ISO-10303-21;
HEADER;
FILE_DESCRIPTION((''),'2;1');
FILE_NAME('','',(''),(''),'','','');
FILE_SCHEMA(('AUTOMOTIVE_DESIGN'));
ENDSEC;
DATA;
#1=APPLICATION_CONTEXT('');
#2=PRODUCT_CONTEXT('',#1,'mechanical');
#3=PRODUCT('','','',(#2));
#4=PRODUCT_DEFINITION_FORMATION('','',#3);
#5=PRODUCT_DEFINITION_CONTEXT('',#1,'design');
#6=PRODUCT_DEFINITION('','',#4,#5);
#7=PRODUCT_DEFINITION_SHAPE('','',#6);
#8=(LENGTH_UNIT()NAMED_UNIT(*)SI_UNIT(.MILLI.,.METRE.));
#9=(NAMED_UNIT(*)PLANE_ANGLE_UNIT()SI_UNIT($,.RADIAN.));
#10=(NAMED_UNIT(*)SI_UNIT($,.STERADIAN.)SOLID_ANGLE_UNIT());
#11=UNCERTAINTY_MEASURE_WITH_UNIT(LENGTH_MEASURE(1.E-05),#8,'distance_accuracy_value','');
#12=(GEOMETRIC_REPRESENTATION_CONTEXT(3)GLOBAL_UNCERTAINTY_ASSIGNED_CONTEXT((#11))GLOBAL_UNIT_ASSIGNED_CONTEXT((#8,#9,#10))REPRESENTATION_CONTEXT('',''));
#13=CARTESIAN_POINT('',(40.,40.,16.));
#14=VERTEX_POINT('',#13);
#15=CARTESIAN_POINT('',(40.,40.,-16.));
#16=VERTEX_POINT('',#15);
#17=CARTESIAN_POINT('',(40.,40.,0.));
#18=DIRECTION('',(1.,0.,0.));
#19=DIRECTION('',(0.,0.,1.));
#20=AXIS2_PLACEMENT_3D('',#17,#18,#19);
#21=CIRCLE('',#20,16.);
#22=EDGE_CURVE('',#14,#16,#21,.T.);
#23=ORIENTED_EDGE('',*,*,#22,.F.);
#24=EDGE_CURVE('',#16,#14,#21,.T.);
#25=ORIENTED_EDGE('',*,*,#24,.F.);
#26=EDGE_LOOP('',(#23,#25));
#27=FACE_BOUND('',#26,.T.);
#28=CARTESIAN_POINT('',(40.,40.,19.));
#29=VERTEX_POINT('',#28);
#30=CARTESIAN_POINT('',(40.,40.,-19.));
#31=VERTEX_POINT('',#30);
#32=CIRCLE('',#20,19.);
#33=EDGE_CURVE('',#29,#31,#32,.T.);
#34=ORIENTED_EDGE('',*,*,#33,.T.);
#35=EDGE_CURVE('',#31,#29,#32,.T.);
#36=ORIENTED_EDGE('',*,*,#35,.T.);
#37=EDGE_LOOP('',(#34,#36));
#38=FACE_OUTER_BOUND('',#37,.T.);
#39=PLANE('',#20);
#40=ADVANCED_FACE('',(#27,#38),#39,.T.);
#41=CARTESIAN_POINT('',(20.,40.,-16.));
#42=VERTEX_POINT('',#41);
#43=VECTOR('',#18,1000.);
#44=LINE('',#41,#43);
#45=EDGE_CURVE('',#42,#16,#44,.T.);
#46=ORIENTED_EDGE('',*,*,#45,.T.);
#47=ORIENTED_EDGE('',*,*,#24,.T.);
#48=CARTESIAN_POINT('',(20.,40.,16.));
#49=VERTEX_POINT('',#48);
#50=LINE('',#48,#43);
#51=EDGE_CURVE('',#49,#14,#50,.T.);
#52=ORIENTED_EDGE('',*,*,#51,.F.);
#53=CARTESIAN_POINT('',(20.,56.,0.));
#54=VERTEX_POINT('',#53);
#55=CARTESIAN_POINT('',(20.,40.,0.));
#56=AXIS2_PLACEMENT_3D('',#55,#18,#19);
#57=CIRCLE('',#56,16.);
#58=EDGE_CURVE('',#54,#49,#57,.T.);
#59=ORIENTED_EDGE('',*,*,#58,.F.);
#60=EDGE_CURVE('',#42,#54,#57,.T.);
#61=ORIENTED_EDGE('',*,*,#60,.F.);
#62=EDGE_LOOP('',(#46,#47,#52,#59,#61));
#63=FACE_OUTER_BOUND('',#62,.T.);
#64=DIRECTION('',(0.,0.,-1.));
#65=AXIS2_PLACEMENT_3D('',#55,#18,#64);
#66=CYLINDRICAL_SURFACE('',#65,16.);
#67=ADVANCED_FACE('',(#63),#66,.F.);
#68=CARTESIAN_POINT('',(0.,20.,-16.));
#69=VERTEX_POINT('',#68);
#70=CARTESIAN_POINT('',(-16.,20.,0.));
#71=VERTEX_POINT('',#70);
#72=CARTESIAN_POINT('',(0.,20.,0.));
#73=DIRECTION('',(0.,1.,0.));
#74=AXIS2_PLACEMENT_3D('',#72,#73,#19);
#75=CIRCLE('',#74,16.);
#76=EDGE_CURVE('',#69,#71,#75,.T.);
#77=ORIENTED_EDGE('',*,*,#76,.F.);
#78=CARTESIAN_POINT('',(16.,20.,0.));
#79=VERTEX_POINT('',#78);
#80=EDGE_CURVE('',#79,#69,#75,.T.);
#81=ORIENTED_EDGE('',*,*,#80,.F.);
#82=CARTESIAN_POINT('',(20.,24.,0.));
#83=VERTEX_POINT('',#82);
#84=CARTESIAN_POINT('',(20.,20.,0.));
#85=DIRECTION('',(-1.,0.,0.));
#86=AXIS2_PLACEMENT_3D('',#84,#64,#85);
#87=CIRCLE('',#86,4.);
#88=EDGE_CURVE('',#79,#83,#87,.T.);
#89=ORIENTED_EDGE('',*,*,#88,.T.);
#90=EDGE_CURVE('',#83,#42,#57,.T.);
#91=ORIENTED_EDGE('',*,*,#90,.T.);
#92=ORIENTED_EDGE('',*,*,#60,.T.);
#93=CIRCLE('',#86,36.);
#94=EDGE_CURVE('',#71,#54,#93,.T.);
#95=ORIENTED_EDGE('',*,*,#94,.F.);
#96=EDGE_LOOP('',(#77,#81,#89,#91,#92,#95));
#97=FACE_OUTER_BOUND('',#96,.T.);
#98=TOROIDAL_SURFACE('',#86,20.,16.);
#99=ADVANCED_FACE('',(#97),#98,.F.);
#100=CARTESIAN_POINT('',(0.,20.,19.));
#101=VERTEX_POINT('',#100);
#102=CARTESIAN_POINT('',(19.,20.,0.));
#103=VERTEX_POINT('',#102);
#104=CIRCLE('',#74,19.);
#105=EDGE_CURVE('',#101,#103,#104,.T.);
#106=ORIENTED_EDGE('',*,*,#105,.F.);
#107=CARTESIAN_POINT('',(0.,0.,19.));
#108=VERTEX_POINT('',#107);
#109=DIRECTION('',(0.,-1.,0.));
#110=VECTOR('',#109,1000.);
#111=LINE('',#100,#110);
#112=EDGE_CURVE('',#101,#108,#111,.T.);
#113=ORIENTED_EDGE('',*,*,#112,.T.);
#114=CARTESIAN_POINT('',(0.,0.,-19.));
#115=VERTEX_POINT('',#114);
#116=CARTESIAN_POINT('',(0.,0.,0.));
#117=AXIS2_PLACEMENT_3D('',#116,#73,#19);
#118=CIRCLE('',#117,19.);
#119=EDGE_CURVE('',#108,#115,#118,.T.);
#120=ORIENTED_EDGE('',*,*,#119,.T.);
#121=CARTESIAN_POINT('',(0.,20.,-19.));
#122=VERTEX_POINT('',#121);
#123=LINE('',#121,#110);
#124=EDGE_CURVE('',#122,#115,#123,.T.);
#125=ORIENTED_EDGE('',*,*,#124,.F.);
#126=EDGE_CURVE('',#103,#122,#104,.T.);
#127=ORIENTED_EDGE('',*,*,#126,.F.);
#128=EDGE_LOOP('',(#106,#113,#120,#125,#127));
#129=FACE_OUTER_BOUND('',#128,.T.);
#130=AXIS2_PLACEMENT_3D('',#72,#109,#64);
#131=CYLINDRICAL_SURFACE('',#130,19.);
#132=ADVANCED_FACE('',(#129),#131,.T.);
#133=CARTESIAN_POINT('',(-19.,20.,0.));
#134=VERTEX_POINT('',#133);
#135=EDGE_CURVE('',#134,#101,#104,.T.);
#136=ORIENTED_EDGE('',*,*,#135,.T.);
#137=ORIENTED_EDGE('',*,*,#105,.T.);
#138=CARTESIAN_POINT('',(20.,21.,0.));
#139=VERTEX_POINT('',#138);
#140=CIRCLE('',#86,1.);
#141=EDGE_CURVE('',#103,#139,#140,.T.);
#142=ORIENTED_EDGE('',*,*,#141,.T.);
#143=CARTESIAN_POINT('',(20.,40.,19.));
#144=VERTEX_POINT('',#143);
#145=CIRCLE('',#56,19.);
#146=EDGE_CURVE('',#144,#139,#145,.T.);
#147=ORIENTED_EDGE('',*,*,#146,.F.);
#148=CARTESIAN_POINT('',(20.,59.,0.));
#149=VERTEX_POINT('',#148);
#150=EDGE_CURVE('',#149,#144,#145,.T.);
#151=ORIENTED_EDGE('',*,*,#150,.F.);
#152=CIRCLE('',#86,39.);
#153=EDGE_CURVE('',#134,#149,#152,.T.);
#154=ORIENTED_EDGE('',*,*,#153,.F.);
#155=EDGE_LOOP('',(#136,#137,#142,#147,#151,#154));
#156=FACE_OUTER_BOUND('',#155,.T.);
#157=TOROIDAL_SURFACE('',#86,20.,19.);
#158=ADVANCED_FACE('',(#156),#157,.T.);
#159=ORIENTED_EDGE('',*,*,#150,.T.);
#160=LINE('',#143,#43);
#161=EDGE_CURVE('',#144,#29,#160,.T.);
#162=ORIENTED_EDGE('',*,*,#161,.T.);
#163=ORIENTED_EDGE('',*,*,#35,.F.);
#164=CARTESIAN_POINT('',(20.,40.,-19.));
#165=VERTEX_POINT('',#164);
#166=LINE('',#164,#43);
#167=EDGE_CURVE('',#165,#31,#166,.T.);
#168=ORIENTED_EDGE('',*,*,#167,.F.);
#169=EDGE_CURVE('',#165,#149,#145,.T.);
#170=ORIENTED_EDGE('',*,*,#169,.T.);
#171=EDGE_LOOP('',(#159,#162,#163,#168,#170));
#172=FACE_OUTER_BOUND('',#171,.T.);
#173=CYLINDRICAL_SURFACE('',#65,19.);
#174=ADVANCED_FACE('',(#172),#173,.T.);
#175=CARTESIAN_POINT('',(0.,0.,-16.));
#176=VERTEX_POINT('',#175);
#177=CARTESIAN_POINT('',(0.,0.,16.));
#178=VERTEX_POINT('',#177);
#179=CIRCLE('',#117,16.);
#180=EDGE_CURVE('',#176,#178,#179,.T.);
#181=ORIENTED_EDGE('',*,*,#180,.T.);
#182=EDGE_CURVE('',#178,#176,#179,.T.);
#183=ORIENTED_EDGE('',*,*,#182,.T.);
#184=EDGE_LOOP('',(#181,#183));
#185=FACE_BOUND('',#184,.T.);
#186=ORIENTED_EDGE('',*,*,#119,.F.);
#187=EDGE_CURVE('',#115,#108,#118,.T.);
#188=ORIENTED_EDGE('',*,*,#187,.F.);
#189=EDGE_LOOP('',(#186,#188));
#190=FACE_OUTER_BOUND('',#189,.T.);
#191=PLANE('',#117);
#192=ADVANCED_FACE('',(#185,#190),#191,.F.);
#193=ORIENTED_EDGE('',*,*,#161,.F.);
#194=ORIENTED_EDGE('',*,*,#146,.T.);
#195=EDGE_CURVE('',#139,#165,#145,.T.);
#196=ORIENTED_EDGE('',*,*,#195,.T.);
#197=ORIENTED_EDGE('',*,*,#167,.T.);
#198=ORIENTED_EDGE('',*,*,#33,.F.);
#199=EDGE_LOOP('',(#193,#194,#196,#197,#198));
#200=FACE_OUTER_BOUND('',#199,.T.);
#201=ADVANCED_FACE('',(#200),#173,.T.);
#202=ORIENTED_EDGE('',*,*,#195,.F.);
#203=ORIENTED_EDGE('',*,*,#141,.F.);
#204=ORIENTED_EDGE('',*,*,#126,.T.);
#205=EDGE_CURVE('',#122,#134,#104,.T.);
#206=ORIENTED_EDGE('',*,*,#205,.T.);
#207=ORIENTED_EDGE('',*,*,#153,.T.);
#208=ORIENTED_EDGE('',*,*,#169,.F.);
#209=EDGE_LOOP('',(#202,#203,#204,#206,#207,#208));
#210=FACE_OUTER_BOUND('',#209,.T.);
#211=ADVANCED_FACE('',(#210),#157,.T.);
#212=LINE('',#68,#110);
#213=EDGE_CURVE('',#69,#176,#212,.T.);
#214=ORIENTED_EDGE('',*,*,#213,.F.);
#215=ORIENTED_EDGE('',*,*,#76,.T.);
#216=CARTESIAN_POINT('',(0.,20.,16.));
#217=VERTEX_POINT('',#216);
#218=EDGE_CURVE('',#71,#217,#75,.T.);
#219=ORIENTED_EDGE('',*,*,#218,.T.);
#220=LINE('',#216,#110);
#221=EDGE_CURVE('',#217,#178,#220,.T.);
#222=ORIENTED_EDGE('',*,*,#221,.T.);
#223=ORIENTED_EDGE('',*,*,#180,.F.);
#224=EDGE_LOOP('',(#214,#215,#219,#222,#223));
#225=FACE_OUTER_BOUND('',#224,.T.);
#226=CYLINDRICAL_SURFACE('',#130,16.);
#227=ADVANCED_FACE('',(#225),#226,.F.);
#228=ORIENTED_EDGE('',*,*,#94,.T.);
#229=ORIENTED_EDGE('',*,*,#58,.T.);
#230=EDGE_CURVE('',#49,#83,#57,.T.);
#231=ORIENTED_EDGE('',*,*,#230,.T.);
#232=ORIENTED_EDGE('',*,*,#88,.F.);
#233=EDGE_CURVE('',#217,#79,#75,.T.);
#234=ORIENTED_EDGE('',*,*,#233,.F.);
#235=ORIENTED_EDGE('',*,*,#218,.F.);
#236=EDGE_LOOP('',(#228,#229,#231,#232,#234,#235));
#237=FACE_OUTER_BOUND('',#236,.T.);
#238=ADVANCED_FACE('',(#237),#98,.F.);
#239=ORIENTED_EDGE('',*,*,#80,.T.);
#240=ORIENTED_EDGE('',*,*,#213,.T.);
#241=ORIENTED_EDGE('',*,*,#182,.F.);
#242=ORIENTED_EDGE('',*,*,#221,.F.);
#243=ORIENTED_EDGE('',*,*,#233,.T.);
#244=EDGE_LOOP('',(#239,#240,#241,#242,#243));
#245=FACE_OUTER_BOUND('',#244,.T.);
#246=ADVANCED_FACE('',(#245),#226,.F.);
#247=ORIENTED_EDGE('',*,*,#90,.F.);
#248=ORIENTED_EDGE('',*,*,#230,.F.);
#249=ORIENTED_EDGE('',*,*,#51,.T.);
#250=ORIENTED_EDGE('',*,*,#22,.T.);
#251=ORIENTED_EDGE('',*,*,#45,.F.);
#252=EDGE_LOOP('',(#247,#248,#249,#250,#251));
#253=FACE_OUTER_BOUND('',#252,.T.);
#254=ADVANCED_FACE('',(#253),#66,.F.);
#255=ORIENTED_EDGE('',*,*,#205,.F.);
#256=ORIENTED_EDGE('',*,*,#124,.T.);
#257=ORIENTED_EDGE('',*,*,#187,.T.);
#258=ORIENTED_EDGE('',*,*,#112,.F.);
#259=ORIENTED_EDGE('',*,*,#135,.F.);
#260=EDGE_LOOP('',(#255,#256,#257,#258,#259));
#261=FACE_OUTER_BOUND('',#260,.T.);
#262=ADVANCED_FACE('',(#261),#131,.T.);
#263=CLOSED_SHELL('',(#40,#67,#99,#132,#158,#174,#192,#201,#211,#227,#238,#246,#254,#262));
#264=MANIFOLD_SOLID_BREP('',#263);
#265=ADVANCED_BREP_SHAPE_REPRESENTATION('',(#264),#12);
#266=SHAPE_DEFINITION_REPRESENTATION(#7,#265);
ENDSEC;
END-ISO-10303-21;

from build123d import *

# Parameters (mm, degrees)
SKETCH_2_R   = 19
SKETCH_2_R_2 = 16


with BuildPart() as part:
    # 扫描1: sweep along a path in 草图1
    with BuildLine(Plane.XY) as sweep_1_path:
        Line((0, 0), (0, 20))
        ThreePointArc((0, 20), (5.857864376, 34.142135624), (20, 40))
        Line((20, 40), (40, 40))
    # 草图2 → 扫描1 (sweep)
    with BuildSketch(Plane(origin=(0, 0, 0), x_dir=(1, 0, 0), z_dir=(0, 1, 0))):
        Circle(SKETCH_2_R)
        Circle(SKETCH_2_R_2, mode=Mode.SUBTRACT)
    sweep(path=sweep_1_path.line)


solid = part.part
